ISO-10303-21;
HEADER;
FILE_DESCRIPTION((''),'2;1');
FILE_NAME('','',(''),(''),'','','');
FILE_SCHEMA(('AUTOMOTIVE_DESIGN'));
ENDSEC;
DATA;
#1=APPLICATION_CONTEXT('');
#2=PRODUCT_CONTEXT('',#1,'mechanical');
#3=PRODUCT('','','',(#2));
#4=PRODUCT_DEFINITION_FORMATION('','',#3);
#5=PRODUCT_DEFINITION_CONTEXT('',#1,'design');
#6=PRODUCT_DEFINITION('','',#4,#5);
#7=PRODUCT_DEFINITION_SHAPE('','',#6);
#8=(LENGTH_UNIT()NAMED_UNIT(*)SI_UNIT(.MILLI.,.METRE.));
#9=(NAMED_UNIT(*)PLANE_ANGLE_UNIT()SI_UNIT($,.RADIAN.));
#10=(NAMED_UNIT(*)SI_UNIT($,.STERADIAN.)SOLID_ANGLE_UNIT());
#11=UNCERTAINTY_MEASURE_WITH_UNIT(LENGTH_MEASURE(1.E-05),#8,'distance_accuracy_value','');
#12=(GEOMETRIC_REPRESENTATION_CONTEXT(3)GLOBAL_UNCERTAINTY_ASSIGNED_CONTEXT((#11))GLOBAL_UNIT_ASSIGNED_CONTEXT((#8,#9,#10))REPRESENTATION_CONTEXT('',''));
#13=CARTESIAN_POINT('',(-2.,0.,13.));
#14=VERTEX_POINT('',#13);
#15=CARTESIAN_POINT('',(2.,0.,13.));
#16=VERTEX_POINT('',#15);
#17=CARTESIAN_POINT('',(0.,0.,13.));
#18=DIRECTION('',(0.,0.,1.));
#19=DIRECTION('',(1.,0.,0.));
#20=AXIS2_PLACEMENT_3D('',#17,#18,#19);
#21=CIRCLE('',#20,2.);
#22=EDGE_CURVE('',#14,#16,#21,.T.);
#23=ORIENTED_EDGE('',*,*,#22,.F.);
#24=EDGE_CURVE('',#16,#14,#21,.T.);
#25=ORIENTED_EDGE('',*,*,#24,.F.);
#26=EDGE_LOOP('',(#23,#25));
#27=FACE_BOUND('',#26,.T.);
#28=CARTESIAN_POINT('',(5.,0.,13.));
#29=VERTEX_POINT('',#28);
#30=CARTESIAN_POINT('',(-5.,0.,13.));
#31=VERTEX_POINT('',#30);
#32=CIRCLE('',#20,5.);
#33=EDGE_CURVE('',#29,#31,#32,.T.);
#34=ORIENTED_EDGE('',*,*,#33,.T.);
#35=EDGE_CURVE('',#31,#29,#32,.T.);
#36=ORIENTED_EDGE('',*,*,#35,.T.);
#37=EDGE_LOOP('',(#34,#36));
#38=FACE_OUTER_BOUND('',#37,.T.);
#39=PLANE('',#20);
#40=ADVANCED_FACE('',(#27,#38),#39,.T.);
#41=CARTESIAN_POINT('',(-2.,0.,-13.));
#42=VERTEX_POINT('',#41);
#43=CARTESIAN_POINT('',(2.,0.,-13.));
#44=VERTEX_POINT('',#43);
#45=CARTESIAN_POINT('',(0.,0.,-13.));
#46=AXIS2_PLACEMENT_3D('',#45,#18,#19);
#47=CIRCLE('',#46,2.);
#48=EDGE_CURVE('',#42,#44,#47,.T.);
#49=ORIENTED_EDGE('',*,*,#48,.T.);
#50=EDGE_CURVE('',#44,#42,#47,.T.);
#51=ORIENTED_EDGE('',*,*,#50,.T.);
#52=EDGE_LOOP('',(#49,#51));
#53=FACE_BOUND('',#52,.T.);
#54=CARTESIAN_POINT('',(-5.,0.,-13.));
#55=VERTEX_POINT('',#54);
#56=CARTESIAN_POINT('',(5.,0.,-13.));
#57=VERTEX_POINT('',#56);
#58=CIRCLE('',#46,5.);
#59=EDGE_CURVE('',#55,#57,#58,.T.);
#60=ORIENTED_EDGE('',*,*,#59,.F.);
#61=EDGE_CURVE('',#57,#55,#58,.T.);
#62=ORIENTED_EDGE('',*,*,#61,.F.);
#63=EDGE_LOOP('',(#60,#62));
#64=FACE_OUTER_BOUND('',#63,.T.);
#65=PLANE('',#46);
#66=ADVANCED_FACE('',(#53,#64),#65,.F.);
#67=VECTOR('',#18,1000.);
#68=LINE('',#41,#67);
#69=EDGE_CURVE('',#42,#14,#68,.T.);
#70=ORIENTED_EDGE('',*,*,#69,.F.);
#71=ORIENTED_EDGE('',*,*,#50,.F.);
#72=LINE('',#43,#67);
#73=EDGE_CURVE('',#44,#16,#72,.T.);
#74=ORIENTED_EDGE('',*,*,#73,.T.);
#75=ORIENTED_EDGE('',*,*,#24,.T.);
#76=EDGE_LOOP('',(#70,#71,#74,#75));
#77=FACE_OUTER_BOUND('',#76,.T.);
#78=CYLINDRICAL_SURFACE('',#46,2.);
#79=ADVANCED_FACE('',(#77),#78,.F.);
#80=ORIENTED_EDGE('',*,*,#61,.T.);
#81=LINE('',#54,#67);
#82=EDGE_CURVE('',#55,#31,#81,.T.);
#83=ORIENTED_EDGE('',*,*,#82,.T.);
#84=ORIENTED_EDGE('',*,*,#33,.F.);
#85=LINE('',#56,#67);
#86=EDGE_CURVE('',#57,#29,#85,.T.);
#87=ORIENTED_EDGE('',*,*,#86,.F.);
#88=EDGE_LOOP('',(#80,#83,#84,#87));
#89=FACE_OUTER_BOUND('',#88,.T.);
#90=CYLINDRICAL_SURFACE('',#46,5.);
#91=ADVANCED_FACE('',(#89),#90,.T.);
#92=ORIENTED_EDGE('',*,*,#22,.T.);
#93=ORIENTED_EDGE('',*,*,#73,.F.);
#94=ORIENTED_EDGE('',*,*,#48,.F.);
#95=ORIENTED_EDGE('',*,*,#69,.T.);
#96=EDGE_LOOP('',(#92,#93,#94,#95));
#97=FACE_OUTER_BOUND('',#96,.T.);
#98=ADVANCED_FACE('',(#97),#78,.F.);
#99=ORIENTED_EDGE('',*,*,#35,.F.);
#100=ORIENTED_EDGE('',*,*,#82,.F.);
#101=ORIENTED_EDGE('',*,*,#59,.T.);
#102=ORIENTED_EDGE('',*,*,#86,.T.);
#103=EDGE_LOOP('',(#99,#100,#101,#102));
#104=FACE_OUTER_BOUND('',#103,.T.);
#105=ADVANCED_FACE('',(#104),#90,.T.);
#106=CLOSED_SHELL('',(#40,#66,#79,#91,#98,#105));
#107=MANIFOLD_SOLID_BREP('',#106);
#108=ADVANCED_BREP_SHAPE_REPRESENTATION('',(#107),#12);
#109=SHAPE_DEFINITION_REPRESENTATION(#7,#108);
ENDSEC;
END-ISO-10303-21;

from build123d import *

# Parameters (mm, degrees)
SKETCH_1_R      = 5
SKETCH_1_R_2    = 2
EXTRUDE_1_DEPTH = 13


with BuildPart() as part:
    # 草图1 → 凸台-拉伸1 (new, symmetric)
    with BuildSketch(Plane.XY):
        Circle(SKETCH_1_R)
        Circle(SKETCH_1_R_2, mode=Mode.SUBTRACT)
    extrude(amount=EXTRUDE_1_DEPTH, both=True)


solid = part.part
